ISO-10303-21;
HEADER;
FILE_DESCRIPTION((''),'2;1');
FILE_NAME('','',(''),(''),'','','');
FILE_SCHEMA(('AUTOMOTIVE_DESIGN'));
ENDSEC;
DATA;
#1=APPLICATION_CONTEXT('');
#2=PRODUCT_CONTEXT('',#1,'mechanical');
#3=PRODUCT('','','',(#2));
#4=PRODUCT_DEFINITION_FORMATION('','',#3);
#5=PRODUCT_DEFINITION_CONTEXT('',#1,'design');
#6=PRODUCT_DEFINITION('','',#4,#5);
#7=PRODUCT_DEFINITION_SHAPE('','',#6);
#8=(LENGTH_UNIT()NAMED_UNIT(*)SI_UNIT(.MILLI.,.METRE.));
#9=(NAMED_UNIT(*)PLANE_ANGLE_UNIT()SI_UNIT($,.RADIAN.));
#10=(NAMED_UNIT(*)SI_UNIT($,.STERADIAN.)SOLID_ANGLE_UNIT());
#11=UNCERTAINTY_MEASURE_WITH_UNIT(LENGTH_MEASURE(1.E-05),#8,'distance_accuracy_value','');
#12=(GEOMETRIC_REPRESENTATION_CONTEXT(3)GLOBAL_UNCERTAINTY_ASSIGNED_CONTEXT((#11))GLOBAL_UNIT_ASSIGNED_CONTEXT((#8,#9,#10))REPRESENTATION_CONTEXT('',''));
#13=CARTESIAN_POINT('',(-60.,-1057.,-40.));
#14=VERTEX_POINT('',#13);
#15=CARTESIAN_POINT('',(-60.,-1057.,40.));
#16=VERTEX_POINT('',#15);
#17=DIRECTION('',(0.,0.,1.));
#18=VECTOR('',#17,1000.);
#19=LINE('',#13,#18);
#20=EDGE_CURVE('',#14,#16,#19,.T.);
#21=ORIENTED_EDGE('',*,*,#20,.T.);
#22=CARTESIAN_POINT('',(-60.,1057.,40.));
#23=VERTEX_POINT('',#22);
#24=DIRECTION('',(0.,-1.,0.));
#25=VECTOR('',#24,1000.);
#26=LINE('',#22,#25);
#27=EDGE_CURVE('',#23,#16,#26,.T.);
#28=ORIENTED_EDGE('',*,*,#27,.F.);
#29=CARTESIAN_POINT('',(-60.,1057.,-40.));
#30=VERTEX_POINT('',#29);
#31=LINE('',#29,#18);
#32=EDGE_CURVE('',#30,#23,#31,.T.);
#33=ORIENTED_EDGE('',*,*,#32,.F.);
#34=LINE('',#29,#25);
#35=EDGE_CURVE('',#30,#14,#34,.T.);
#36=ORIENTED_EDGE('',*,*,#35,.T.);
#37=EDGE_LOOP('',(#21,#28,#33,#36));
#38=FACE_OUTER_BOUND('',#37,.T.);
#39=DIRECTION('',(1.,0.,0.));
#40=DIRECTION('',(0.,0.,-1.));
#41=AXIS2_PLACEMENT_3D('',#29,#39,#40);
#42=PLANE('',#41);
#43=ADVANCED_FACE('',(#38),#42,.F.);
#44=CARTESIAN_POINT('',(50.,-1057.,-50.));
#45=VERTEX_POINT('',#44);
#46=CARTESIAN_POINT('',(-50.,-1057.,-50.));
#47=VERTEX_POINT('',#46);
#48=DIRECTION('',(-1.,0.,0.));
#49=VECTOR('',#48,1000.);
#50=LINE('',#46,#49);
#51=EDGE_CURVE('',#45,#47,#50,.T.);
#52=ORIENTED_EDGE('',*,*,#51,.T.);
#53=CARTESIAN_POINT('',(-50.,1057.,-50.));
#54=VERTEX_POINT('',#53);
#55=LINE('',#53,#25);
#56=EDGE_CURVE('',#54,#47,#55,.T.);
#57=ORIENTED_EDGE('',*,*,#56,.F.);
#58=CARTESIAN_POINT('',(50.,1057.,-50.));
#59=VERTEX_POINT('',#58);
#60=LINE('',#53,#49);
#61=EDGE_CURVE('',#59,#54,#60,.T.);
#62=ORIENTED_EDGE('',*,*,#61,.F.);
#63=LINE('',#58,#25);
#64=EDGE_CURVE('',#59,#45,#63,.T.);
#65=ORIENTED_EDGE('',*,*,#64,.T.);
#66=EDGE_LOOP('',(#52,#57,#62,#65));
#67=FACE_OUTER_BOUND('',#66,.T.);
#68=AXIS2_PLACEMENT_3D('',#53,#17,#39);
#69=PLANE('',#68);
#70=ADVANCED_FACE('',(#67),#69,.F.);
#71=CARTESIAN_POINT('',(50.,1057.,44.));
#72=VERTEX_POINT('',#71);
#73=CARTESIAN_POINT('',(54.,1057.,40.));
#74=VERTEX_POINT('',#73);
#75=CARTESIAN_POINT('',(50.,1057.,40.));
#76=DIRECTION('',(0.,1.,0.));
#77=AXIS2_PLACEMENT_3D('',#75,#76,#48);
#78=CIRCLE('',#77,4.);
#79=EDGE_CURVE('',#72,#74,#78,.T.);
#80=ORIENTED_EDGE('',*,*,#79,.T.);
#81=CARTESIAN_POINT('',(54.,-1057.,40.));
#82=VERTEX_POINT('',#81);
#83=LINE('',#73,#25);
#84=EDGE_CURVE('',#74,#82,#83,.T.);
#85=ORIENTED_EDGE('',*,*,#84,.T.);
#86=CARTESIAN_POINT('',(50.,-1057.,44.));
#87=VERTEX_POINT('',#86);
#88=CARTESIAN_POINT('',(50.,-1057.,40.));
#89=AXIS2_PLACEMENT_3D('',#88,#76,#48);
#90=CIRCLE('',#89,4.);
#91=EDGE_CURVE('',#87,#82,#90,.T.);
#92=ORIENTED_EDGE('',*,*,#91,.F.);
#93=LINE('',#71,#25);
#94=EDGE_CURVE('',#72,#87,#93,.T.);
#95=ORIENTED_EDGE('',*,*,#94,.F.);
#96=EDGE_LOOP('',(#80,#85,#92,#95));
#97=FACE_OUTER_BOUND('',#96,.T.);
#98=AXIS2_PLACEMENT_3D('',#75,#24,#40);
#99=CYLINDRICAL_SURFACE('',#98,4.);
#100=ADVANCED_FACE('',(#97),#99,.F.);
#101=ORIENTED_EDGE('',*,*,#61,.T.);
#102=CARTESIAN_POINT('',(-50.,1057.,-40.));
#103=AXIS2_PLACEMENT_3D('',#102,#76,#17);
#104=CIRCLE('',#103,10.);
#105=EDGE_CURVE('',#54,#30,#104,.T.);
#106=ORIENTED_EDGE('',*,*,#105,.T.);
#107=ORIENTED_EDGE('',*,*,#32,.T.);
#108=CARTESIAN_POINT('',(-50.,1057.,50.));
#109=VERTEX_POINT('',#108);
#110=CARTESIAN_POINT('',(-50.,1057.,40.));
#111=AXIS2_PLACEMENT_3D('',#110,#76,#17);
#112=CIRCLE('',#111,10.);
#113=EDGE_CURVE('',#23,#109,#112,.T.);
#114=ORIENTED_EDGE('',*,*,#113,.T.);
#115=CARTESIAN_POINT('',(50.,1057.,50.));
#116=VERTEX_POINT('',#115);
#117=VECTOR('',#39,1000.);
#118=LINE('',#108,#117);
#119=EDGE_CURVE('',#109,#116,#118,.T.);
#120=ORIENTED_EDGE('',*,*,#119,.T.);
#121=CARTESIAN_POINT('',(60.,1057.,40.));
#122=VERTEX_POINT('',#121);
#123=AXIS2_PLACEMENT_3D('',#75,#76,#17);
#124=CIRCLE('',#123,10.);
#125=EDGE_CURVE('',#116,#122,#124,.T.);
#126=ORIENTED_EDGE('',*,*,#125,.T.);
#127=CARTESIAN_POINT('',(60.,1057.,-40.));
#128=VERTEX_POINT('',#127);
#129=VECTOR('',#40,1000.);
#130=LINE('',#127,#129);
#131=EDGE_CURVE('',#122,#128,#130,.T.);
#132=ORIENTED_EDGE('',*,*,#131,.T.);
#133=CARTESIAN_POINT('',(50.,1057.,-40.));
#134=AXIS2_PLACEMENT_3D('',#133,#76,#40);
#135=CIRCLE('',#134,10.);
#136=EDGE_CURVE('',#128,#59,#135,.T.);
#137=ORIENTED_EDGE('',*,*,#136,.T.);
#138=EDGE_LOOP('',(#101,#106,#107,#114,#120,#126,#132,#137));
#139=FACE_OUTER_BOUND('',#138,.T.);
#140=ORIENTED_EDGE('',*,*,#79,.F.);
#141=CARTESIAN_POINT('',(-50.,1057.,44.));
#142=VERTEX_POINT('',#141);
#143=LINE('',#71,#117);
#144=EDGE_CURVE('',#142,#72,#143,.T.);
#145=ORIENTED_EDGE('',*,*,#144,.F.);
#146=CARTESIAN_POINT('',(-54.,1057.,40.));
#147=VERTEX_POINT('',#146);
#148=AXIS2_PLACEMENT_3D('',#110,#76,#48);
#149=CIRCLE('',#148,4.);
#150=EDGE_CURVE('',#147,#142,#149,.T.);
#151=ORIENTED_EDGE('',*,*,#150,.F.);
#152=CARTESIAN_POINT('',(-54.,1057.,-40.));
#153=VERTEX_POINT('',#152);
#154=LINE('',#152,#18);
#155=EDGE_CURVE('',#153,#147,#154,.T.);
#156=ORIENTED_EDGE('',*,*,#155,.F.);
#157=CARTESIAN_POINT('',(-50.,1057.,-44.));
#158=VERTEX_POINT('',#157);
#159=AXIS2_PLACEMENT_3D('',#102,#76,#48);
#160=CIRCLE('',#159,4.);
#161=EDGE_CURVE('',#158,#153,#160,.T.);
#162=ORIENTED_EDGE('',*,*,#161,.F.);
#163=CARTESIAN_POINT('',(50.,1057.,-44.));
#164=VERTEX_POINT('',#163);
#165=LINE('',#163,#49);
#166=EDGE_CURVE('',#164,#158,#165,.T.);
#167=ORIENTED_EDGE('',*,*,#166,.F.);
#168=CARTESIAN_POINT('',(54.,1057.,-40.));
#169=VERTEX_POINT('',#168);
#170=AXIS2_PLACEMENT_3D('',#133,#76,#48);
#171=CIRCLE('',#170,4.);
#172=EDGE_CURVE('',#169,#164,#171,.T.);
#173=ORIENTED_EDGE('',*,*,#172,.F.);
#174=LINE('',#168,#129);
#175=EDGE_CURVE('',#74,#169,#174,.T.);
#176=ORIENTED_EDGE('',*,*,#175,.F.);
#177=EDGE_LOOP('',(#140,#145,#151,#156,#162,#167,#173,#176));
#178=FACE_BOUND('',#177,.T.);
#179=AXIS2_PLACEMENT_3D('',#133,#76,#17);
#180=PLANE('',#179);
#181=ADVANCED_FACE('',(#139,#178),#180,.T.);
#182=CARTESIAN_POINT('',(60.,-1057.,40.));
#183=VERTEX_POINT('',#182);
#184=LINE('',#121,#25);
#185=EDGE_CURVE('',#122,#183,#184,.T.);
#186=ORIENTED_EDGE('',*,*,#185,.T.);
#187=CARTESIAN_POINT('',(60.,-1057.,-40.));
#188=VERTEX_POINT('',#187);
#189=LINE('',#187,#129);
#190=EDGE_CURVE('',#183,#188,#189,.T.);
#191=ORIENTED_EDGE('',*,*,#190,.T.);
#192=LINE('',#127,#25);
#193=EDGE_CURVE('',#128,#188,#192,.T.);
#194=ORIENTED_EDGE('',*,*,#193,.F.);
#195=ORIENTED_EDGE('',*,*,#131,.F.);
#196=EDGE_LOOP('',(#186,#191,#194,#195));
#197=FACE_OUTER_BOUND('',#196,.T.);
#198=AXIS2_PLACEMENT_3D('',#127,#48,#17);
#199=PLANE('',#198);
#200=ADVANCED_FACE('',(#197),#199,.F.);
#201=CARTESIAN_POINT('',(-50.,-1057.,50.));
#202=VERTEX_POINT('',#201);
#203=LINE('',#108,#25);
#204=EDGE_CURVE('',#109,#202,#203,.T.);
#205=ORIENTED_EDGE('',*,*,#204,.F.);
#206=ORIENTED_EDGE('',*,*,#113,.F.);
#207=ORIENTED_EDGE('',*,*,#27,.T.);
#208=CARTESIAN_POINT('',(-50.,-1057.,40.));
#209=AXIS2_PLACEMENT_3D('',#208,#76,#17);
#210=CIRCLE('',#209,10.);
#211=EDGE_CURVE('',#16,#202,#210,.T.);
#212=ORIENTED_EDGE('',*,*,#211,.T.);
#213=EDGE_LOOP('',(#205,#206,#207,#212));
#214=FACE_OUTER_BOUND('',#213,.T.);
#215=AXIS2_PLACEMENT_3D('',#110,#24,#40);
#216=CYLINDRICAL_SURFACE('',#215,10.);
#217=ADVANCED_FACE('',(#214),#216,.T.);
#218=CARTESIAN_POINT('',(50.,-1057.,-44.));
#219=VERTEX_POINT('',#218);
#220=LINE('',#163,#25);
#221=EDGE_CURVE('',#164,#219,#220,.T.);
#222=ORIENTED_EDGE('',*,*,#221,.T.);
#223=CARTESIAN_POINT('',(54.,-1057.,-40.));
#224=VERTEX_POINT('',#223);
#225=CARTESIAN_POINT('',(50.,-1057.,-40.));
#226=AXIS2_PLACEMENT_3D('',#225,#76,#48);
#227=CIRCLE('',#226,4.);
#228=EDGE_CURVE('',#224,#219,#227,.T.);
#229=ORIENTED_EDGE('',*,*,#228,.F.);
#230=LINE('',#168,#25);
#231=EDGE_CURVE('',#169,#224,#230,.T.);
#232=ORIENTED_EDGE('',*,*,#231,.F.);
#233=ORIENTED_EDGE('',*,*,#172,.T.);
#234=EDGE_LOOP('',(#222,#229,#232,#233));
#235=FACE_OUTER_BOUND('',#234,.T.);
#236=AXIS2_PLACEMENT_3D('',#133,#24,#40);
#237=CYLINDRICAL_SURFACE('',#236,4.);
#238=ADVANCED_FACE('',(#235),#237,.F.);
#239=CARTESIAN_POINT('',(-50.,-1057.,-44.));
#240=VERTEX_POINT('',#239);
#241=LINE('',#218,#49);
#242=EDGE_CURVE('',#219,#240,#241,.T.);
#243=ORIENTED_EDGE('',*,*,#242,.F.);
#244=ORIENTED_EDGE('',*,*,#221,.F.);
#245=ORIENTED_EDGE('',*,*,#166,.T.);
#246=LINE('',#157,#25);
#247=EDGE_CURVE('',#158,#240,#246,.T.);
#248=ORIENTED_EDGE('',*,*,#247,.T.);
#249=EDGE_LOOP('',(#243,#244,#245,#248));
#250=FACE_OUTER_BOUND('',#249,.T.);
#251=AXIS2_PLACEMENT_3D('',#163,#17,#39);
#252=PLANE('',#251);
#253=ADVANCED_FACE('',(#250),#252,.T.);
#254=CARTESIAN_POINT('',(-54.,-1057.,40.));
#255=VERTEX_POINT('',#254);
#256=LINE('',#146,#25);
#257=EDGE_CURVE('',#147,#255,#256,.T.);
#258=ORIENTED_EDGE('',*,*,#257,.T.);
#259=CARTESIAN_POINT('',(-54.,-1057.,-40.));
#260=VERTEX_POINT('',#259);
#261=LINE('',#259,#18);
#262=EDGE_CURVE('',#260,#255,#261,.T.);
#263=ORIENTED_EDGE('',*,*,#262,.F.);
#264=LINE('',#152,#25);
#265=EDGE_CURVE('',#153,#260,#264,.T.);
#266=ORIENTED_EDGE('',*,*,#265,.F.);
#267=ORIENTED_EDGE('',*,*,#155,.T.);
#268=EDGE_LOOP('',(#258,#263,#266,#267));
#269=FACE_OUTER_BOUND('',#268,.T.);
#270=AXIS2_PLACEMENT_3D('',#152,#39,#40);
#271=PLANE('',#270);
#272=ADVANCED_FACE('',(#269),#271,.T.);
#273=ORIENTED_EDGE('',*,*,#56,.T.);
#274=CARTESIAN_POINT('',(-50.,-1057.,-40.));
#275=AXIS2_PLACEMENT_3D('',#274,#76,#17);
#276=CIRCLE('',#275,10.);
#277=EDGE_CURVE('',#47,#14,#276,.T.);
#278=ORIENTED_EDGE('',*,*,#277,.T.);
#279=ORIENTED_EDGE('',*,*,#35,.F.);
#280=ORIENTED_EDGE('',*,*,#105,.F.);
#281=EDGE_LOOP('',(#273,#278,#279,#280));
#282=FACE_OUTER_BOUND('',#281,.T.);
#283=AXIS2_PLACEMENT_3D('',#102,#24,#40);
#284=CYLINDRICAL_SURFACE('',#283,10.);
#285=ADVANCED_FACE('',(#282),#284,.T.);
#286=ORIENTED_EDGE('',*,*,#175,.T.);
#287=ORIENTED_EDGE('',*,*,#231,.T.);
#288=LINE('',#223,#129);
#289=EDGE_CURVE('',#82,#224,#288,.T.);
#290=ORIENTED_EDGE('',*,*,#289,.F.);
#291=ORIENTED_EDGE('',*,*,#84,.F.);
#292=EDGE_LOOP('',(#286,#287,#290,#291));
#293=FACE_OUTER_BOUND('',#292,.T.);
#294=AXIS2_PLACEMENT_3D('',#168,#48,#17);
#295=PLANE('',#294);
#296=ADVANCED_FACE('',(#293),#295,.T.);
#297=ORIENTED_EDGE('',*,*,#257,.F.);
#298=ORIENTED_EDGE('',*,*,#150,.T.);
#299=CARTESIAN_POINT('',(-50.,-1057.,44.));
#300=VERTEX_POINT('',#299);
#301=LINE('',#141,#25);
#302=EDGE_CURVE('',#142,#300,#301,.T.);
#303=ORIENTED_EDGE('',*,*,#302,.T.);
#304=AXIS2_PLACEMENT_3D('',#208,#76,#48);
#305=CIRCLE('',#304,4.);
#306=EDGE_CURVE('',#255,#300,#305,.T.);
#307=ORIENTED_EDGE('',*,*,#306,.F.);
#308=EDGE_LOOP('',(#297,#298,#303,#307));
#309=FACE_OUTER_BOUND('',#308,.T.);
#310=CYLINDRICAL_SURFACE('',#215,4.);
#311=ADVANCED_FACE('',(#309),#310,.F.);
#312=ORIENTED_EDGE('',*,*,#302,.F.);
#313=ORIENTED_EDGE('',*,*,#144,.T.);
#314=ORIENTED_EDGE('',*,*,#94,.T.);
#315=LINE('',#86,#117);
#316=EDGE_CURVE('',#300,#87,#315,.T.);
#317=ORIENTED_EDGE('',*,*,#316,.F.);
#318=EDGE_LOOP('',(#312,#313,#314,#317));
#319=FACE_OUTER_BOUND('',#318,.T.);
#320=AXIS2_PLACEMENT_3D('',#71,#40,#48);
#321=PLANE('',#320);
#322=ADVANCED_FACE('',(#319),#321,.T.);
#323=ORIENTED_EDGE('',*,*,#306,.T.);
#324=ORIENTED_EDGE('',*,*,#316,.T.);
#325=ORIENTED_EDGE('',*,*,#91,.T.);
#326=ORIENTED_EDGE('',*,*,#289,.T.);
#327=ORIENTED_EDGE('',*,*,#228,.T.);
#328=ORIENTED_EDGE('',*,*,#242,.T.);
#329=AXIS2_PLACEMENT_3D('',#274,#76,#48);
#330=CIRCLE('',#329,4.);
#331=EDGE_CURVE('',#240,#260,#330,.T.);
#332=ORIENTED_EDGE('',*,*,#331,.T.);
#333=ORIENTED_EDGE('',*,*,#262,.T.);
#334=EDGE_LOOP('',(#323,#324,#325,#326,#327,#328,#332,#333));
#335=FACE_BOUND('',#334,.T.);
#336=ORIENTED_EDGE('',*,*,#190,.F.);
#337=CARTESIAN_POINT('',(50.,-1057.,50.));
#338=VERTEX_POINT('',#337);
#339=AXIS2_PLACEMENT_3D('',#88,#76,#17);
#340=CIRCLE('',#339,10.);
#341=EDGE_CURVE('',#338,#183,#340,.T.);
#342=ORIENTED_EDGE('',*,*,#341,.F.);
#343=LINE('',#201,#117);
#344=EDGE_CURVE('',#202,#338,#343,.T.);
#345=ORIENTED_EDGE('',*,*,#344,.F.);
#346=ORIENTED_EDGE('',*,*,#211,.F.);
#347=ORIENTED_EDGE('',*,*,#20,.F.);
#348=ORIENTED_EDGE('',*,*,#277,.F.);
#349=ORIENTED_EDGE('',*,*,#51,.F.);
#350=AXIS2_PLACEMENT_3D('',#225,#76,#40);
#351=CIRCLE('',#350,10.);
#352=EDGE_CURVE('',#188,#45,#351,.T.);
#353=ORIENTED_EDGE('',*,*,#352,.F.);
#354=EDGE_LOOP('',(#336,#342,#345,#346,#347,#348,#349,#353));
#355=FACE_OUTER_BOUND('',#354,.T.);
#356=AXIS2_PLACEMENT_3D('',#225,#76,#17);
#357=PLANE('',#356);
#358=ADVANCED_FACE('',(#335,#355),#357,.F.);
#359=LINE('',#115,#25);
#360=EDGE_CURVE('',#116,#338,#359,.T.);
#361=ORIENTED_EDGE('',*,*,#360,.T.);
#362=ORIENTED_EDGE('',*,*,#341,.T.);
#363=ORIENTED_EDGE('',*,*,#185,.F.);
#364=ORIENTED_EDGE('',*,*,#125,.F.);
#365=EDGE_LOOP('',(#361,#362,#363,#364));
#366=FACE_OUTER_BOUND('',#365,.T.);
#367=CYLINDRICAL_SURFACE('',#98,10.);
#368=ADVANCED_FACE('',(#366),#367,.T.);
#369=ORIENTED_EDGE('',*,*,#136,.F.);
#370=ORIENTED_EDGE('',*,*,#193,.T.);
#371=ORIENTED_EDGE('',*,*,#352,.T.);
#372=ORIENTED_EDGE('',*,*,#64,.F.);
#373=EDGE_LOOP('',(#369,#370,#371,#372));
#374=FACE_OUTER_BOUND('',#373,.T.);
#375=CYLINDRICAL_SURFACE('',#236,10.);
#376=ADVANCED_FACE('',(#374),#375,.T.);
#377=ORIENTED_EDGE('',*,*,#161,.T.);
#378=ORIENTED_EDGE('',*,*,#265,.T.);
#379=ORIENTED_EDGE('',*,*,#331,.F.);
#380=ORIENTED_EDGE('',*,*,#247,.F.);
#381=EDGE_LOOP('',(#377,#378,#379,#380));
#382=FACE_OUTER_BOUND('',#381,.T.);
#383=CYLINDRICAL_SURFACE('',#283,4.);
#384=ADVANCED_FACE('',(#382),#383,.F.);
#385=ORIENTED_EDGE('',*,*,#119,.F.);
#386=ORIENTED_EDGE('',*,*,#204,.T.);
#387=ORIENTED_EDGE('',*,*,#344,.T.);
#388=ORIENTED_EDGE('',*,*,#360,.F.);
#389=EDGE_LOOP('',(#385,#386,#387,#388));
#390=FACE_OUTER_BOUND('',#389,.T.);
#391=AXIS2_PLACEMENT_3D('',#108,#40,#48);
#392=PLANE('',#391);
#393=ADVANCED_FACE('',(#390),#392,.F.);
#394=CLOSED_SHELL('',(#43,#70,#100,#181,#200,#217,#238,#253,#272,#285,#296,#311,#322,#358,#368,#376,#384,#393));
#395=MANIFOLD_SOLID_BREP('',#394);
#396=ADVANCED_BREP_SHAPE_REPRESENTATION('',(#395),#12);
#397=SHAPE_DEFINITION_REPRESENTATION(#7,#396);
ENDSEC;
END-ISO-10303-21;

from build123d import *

# Parameters (mm, degrees)
EXTRUDE_THIN1_DEPTH = 1057


with BuildPart() as part:
    # Sketch1 → Extrude-Thin1 (new, symmetric)
    with BuildSketch(Plane(origin=(0, 0, 0), x_dir=(1, 0, 0), z_dir=(0, 1, 0))):
        with BuildLine():
            Line((-50, 50), (50, 50))
            ThreePointArc((50, 50), (57.071067812, 47.071067812), (60, 40))
            Line((60, 40), (60, -40))
            ThreePointArc((60, -40), (57.071067812, -47.071067812), (50, -50))
            Line((50, -50), (-50, -50))
            ThreePointArc((-50, -50), (-57.071067812, -47.071067812), (-60, -40))
            Line((-60, -40), (-60, 40))
            ThreePointArc((-60, 40), (-57.071067812, 47.071067812), (-50, 50))
        make_face()
        with BuildLine():
            Line((-50, 44), (50, 44))
            ThreePointArc((50, 44), (52.828427125, 42.828427125), (54, 40))
            Line((54, 40), (54, -40))
            ThreePointArc((54, -40), (52.828427125, -42.828427125), (50, -44))
            Line((50, -44), (-50, -44))
            ThreePointArc((-50, -44), (-52.828427125, -42.828427125), (-54, -40))
            Line((-54, -40), (-54, 40))
            ThreePointArc((-54, 40), (-52.828427125, 42.828427125), (-50, 44))
        make_face(mode=Mode.SUBTRACT)
    extrude(amount=EXTRUDE_THIN1_DEPTH, both=True)


solid = part.part
